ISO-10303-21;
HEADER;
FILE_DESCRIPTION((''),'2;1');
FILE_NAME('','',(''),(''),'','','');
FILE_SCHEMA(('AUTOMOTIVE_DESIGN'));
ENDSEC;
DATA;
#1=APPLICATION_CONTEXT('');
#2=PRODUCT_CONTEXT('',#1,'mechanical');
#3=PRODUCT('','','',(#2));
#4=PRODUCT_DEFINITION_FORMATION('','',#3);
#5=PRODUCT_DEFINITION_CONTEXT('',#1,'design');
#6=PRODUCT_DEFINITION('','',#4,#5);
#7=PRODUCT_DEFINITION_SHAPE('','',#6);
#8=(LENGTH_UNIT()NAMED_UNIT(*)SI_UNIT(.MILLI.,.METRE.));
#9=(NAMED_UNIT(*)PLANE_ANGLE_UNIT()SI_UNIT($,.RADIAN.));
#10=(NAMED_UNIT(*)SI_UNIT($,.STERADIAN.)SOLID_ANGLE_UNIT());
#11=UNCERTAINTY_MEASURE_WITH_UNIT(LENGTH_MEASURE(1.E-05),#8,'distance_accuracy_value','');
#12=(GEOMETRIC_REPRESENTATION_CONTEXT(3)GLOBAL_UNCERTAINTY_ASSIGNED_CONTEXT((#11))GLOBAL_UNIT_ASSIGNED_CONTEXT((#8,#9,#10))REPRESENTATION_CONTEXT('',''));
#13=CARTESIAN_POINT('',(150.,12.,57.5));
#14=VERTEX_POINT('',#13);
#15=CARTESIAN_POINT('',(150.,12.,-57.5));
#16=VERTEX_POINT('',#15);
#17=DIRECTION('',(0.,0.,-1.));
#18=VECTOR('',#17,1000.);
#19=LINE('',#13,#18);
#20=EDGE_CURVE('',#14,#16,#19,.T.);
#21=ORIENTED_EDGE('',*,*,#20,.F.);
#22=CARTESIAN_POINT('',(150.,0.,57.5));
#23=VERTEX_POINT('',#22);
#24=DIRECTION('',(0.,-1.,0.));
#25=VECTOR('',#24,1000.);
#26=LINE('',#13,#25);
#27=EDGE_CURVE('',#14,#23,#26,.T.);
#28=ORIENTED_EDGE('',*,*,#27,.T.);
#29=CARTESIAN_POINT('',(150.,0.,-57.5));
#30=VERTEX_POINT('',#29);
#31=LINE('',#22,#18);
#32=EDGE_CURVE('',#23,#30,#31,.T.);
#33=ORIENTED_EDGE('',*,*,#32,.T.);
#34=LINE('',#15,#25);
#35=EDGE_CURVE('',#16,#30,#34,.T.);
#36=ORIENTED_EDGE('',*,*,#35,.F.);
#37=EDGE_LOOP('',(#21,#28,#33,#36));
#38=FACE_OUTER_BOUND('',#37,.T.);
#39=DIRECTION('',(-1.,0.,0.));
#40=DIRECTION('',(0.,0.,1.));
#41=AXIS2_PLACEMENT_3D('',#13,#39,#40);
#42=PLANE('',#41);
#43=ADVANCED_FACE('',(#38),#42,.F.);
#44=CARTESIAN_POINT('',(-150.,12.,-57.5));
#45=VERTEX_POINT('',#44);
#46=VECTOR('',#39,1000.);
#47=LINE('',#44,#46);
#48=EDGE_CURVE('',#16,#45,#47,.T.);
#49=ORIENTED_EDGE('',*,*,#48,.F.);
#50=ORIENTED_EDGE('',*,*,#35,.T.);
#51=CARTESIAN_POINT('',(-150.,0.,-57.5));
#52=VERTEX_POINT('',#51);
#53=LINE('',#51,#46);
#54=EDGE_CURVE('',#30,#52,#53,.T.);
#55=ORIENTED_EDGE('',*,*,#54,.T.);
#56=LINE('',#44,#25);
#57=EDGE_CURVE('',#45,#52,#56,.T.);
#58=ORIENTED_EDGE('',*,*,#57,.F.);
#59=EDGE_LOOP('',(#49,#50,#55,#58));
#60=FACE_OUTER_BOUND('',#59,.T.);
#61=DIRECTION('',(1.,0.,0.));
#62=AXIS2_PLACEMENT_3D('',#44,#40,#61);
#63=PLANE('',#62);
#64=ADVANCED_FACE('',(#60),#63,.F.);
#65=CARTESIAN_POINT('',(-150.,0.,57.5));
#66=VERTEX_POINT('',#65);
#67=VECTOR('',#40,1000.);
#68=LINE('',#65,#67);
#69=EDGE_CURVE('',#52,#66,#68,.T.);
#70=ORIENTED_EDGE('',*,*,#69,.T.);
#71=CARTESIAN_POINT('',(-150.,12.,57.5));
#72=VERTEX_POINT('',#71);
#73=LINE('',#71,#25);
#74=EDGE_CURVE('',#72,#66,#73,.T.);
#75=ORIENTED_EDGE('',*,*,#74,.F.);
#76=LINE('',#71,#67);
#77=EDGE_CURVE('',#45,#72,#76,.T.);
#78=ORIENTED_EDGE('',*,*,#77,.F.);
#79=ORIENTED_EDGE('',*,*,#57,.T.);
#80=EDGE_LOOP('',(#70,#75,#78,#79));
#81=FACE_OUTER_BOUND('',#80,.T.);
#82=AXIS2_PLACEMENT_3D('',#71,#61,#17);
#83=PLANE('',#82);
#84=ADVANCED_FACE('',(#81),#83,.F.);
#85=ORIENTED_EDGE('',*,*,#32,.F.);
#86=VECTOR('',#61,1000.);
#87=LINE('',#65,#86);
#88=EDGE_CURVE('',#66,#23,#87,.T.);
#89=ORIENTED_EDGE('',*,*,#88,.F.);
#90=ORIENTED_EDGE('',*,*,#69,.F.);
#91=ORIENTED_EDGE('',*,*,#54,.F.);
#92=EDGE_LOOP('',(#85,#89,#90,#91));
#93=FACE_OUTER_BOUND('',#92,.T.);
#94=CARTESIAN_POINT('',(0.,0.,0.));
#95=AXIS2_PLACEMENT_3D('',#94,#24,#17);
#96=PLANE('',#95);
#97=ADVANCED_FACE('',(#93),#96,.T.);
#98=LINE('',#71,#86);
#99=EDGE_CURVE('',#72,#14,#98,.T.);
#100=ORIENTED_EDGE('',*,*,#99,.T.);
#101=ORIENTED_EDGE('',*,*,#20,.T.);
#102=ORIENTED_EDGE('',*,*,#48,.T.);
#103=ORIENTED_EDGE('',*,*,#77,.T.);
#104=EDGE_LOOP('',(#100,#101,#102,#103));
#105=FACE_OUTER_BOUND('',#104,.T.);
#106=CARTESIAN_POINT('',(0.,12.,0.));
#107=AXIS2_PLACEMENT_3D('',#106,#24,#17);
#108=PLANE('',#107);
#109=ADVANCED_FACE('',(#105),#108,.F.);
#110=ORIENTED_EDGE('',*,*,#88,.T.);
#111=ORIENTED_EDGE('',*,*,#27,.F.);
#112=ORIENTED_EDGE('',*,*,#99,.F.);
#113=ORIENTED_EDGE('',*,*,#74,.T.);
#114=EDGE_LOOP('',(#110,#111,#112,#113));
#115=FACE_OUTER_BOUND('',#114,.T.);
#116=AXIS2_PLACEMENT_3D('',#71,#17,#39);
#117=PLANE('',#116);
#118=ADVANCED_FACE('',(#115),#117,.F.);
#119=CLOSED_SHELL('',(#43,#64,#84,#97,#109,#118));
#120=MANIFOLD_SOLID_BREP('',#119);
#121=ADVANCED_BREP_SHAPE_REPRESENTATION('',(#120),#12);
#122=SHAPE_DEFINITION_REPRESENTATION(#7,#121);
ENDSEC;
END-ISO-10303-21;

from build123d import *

# Parameters (mm, degrees)
SKETCH_1_W      = 300
SKETCH_1_H      = 115
EXTRUDE_1_DEPTH = 12


with BuildPart() as part:
    # 草图1 → 凸台-拉伸1 (new body)
    with BuildSketch(Plane(origin=(0, 0, 0), x_dir=(1, 0, 0), z_dir=(0, 1, 0))):
        Rectangle(SKETCH_1_W, SKETCH_1_H)
    extrude(amount=EXTRUDE_1_DEPTH)


solid = part.part
